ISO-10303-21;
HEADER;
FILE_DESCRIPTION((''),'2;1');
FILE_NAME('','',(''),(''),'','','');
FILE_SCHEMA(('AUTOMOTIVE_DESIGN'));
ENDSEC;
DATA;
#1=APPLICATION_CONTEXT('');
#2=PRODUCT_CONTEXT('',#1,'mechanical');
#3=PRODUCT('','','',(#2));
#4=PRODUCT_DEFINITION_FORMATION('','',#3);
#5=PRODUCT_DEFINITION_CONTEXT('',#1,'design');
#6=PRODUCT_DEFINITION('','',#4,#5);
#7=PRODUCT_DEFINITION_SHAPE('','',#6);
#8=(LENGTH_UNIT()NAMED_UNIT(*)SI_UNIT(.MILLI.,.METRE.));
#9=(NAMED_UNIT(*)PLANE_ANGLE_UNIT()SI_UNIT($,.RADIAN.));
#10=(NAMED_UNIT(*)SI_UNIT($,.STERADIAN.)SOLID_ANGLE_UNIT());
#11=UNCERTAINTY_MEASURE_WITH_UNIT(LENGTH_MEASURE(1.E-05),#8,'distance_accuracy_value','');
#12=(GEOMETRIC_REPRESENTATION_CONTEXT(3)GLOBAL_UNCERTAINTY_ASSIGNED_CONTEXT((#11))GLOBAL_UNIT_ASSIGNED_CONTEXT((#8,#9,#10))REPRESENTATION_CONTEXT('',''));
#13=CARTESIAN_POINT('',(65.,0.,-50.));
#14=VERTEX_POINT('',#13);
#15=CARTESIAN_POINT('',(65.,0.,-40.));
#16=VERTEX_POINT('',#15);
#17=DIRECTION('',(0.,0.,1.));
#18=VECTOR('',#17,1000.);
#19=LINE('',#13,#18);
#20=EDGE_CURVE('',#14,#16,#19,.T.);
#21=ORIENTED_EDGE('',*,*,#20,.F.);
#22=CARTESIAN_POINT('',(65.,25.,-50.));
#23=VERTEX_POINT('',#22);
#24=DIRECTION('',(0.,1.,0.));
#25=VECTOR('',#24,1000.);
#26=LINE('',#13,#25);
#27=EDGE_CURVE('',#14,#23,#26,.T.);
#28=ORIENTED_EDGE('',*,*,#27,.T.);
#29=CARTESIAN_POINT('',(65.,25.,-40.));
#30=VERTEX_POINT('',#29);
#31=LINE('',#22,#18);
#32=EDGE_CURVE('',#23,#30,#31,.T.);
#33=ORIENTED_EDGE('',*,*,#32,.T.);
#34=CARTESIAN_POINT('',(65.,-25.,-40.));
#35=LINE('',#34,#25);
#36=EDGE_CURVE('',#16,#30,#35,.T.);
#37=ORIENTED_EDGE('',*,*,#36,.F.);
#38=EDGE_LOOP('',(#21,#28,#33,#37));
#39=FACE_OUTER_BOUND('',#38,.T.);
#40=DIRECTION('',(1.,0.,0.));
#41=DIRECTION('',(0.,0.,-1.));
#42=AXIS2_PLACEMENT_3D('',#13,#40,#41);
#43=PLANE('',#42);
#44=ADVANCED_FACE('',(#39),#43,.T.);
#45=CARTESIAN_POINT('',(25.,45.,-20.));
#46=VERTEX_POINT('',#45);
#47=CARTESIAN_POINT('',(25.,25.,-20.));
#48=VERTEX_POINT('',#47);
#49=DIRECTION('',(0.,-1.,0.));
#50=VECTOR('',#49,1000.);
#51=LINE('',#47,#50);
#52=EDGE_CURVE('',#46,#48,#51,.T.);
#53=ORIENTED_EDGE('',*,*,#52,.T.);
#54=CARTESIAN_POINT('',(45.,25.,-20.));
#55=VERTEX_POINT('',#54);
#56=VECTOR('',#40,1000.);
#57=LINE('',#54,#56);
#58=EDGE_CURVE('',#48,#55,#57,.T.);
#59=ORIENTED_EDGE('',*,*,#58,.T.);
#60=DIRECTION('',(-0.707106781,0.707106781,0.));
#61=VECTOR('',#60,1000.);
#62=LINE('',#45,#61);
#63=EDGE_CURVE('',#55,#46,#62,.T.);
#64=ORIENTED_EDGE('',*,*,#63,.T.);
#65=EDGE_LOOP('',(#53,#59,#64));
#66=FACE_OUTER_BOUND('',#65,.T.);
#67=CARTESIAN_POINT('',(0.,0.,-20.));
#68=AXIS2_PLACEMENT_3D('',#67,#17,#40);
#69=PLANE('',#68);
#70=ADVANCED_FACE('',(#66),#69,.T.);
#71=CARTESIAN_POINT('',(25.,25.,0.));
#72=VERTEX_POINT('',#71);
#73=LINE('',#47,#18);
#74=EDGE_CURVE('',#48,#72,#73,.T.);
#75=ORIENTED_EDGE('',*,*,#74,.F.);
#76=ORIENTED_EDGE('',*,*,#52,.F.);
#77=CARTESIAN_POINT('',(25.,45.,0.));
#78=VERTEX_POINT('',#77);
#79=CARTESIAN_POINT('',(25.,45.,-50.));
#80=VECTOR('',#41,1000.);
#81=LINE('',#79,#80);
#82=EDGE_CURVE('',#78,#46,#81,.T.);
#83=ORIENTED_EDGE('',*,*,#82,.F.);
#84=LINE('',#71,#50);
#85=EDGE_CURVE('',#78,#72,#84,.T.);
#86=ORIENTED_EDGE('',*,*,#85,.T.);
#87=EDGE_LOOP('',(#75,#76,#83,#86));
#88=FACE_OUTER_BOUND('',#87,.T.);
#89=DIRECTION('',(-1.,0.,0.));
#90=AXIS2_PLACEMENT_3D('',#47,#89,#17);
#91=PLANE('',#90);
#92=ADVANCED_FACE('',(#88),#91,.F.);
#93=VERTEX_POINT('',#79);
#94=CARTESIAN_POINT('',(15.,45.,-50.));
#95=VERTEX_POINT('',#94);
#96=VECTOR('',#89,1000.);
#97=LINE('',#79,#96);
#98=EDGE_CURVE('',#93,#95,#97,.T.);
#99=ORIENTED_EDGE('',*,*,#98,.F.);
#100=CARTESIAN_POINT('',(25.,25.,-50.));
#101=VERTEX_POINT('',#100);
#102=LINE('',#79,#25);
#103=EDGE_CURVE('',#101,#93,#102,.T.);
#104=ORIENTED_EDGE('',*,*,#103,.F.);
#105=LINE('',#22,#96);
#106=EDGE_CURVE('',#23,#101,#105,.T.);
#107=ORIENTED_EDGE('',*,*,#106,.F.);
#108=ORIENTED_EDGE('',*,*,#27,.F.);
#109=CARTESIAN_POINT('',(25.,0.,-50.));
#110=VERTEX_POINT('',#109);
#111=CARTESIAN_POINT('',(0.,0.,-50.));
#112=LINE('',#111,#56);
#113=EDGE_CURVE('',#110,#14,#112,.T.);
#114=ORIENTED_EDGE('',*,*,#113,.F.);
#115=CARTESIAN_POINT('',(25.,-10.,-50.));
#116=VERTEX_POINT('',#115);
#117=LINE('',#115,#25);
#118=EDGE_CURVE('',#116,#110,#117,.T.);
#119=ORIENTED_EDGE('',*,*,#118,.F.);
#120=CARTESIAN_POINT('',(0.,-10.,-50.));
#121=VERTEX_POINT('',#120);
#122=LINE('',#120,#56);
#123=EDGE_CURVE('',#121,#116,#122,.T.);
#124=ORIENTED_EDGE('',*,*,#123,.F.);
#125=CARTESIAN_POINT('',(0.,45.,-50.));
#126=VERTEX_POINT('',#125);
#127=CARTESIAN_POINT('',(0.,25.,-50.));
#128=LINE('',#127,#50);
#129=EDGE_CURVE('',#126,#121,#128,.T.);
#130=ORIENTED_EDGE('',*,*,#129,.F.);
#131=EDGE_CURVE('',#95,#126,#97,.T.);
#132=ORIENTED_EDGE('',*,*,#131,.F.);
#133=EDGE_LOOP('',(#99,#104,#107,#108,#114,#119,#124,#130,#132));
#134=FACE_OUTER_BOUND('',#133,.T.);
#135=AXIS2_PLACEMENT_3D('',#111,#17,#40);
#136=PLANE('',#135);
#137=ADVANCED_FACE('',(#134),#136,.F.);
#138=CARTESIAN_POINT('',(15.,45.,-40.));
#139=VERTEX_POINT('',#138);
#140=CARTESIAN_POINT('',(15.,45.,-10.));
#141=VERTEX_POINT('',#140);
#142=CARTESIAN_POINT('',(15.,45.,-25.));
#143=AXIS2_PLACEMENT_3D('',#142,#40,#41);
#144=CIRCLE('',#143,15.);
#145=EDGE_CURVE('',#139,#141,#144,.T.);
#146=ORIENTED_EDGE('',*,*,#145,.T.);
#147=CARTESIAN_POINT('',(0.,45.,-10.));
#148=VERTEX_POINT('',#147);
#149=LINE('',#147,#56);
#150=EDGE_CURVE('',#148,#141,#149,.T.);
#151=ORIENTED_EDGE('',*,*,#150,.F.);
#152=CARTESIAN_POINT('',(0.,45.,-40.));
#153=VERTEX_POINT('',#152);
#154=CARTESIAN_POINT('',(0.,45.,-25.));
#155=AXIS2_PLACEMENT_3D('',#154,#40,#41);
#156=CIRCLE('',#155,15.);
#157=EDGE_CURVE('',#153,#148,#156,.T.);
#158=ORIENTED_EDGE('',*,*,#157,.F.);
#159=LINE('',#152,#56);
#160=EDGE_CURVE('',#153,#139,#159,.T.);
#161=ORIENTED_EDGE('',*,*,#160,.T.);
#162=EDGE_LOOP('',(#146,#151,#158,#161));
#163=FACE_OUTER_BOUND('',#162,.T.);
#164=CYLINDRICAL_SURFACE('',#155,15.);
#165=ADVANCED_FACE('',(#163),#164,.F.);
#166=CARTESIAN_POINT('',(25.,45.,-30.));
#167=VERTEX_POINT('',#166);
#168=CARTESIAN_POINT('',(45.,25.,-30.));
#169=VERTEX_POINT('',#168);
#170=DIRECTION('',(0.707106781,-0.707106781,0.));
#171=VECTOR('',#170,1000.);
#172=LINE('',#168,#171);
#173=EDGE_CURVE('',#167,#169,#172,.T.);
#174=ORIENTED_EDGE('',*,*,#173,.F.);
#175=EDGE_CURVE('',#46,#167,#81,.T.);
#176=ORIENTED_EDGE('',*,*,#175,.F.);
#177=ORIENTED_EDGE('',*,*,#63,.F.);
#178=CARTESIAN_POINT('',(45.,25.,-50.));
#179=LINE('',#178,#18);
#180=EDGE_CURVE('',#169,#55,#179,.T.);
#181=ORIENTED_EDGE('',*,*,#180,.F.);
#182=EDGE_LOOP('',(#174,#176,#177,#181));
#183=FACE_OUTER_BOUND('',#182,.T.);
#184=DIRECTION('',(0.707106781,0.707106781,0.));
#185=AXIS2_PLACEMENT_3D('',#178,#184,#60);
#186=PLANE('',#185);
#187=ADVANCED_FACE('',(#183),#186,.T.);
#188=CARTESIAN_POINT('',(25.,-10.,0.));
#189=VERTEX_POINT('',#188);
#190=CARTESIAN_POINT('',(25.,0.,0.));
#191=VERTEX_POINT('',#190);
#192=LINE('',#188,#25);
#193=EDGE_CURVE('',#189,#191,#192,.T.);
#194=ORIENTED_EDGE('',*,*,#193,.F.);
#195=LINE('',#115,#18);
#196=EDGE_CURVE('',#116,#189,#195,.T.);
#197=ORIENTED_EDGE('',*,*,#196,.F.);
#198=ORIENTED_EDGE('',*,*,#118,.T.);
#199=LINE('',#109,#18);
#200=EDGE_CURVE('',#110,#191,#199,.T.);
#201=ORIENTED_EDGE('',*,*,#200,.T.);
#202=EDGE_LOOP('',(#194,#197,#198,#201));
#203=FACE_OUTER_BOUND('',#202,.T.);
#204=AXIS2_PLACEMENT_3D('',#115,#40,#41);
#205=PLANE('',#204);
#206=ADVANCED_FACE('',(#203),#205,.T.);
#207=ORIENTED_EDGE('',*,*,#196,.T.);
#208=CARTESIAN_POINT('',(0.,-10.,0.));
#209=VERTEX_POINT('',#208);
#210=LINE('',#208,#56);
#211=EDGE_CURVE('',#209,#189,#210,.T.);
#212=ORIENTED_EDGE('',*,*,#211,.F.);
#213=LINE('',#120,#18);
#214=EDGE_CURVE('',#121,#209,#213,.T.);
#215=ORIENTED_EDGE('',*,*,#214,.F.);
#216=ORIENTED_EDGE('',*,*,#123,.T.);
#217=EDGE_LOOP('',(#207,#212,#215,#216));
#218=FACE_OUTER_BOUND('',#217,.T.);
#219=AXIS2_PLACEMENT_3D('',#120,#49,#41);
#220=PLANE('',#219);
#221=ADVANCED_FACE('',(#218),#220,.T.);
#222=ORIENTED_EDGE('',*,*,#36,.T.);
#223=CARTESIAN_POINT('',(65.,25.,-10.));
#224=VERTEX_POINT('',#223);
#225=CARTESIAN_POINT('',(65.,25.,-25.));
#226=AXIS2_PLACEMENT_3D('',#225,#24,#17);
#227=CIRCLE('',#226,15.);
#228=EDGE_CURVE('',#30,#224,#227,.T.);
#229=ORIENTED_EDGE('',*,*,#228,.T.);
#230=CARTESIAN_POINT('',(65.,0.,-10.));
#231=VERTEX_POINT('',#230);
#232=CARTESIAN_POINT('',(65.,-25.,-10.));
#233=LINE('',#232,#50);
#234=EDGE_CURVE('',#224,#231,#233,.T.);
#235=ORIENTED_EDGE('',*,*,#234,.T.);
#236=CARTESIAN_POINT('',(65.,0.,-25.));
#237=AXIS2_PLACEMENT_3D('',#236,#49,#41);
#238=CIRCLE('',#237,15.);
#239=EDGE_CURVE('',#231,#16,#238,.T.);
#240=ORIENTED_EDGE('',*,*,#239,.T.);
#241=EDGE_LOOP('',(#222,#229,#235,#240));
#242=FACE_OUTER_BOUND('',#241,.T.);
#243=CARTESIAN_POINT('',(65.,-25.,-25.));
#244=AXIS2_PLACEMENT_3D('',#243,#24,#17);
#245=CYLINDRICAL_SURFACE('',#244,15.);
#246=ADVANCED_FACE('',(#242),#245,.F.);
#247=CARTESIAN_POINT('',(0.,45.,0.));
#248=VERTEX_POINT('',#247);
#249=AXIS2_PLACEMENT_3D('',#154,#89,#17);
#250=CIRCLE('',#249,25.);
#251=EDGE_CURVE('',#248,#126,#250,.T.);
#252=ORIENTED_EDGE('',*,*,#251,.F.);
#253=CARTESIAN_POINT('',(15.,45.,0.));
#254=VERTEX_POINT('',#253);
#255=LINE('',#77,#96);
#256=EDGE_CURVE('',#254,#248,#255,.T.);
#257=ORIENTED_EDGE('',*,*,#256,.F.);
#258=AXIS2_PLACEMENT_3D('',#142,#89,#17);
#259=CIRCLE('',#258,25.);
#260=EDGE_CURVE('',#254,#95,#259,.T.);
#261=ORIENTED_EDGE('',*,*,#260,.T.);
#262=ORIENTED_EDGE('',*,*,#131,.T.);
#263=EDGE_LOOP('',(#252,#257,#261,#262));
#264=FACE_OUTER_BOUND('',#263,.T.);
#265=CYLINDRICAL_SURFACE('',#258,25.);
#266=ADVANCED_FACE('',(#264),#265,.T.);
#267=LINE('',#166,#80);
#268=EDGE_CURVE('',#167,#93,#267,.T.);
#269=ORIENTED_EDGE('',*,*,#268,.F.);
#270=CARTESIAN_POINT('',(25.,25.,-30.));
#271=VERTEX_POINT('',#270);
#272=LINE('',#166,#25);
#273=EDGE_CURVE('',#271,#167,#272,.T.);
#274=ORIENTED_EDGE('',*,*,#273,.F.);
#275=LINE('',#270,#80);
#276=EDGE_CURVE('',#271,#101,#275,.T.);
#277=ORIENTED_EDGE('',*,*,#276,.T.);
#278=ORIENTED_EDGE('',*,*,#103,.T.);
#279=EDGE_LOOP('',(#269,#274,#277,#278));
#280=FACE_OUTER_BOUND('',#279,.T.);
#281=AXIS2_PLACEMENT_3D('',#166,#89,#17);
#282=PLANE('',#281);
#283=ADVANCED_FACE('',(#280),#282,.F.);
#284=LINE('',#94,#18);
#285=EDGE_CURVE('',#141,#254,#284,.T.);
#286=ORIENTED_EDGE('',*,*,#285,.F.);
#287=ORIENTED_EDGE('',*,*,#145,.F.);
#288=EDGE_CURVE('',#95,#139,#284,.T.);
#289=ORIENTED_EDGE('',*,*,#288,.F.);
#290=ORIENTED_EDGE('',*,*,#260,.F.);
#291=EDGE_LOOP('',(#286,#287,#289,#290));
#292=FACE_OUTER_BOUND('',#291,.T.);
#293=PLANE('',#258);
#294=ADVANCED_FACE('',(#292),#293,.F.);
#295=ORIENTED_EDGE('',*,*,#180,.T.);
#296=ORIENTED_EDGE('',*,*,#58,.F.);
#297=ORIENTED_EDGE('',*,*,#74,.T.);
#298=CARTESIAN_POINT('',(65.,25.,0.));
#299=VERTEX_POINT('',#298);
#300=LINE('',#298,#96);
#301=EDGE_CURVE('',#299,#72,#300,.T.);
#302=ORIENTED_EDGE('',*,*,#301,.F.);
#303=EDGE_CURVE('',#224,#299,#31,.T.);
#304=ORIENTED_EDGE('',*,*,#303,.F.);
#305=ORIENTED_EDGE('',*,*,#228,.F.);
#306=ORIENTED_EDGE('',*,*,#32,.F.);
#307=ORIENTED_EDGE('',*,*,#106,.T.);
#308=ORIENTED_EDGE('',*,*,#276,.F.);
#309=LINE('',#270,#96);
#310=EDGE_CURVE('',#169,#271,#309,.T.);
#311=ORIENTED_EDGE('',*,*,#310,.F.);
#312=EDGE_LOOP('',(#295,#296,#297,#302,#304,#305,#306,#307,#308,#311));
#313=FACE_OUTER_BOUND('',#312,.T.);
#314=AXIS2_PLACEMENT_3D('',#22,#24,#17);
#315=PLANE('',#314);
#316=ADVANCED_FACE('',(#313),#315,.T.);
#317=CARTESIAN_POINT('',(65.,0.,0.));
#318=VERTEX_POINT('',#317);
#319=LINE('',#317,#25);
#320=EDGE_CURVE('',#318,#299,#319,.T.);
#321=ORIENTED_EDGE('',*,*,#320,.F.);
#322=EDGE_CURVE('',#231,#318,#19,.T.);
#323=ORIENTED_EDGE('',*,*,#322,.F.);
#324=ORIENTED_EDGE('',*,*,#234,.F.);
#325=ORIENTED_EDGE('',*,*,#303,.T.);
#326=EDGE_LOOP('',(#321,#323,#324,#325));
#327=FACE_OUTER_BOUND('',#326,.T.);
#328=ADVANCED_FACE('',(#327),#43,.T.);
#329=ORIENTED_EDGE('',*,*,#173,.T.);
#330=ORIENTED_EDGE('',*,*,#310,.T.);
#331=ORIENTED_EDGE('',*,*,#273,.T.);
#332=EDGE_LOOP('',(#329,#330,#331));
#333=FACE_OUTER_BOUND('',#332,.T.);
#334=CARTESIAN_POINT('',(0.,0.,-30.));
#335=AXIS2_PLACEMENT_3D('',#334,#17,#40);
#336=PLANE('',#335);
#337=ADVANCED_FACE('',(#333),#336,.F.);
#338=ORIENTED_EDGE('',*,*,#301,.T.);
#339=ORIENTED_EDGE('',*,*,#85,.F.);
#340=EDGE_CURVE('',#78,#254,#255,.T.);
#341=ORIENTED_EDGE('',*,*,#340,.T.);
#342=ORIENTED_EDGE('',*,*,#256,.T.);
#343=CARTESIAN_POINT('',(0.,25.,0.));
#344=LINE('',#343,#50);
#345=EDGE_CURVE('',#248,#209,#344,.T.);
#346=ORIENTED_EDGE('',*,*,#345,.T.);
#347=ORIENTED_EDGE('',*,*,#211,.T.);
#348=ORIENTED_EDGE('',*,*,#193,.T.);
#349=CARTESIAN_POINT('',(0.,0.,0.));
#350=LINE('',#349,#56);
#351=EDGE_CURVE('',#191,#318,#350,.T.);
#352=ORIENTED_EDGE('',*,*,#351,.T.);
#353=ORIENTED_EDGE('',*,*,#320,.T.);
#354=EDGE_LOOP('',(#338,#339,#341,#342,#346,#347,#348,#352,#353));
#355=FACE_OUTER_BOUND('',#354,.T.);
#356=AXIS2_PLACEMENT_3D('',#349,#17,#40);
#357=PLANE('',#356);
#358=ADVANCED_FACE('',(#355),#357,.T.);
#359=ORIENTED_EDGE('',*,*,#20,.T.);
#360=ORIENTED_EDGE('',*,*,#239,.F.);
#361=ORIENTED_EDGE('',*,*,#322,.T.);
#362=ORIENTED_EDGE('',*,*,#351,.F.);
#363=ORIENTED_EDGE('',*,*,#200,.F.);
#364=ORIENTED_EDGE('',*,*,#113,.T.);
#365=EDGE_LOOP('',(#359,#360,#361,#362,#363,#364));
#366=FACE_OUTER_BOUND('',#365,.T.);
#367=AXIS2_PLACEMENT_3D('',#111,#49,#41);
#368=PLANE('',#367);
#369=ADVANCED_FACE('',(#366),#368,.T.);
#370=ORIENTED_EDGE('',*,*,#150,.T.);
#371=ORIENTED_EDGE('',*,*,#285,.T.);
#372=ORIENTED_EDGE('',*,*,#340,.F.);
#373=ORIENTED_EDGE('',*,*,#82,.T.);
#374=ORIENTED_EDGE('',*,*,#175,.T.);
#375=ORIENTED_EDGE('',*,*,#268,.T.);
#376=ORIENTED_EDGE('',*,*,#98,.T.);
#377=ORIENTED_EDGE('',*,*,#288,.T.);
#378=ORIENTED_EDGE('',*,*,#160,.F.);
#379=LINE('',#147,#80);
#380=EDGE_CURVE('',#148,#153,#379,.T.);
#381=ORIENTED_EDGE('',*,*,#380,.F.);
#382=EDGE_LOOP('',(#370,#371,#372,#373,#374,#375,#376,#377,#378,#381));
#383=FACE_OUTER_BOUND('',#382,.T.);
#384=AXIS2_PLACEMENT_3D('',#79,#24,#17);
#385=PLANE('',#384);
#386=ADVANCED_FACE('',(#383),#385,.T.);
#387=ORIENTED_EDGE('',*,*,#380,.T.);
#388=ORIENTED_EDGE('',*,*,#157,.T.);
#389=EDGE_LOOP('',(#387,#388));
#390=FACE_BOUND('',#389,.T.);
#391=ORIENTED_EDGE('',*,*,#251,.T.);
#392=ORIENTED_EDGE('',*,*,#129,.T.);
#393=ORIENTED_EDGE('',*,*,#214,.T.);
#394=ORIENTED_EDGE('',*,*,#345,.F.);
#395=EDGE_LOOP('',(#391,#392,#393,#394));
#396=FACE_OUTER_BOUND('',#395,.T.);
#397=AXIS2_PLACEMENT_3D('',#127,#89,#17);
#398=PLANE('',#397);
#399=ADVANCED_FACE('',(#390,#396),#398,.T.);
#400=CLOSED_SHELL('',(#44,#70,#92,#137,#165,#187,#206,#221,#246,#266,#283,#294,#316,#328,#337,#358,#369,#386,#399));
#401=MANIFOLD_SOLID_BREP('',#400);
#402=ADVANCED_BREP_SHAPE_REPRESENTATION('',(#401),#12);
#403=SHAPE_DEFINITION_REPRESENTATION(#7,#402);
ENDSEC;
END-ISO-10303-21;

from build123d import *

# Parameters (mm, degrees)
BASE_BLOCK_PROFILE_W      = 65
BASE_BLOCK_PROFILE_H      = 25
BASE_BLOCK_65X25X50_DEPTH = 50
UPRIGHT_PROFILE_W         = 50
UPRIGHT_PROFILE_H         = 20
UPRIGHT_BLOCK_DEPTH       = 25
BOTTOM_TONGUE_PROFILE_W   = 25
BOTTOM_TONGUE_PROFILE_H   = 10
BOTTOM_TONGUE_10X25_DEPTH = 50
END_NOTCH_PROFILE_R       = 15
ROUND_END_NOTCH_DEPTH     = 50
TOP_BOSS_PROFILE_R        = 25
ROUNDED_TOP_BOSS_DEPTH    = 15
BOSS_HALF_HOLE_15_DEPTH   = 15
SUPPORT_WEDGE_DEPTH       = 50
RIB_TRIM_FRONT_DEPTH      = 20
RIB_TRIM_REAR_DEPTH       = 20


with BuildPart() as part:
    # Base Block Profile → Base Block 65x25x50 (new body)
    with BuildSketch(Plane.XY):
        with Locations((32.5, 12.5)):
            Rectangle(BASE_BLOCK_PROFILE_W, BASE_BLOCK_PROFILE_H)
    extrude(amount=-BASE_BLOCK_65X25X50_DEPTH)

    # Upright Profile → Upright Block (add)
    with BuildSketch(Plane.ZY):
        with Locations((-25, 35)):
            Rectangle(UPRIGHT_PROFILE_W, UPRIGHT_PROFILE_H)
    extrude(amount=-UPRIGHT_BLOCK_DEPTH)

    # Bottom Tongue Profile → Bottom Tongue 10x25 (add)
    with BuildSketch(Plane.XY):
        with Locations((12.5, -5)):
            Rectangle(BOTTOM_TONGUE_PROFILE_W, BOTTOM_TONGUE_PROFILE_H)
    extrude(amount=-BOTTOM_TONGUE_10X25_DEPTH)

    # End Notch Profile → Round End Notch (cut)
    with BuildSketch(Plane(origin=(0, 25, 0), x_dir=(1, 0, 0), z_dir=(0, 1, 0))):
        with Locations((65, 25)):
            Circle(END_NOTCH_PROFILE_R)
    extrude(amount=-ROUND_END_NOTCH_DEPTH, mode=Mode.SUBTRACT)

    # Top Boss Profile → Rounded Top Boss (add)
    with BuildSketch(Plane.ZY):
        with Locations((-25, 45)):
            Circle(TOP_BOSS_PROFILE_R)
    extrude(amount=-ROUNDED_TOP_BOSS_DEPTH)

    # Boss Hole Profile → Boss Half Hole Ø15 (cut)
    with BuildSketch(Plane(origin=(15, 0, 0), x_dir=(0, 0, -1), z_dir=(1, 0, 0))):
        with BuildLine():
            Line((10, 45), (40, 45))
            ThreePointArc((40, 45), (25, 60), (10, 45))
        make_face()
    extrude(amount=-BOSS_HALF_HOLE_15_DEPTH, mode=Mode.SUBTRACT)

    # Support Wedge Profile → Support Wedge (add)
    with BuildSketch(Plane.XY):
        Polygon((25, 45), (25, 25), (45, 25), align=None)
    extrude(amount=-SUPPORT_WEDGE_DEPTH)

    # Rib Trim Front Profile → Rib Trim Front (cut)
    with BuildSketch(Plane.XY):
        Polygon((25, 45), (45, 25), (25, 25), align=None)
    extrude(amount=-RIB_TRIM_FRONT_DEPTH, mode=Mode.SUBTRACT)

    # Rib Trim Rear Profile → Rib Trim Rear (cut)
    with BuildSketch(Plane(origin=(0, 0, -50), x_dir=(-1, 0, 0), z_dir=(0, 0, -1))):
        Polygon((-25, 45), (-25, 25), (-45, 25), align=None)
    extrude(amount=-RIB_TRIM_REAR_DEPTH, mode=Mode.SUBTRACT)


solid = part.part
